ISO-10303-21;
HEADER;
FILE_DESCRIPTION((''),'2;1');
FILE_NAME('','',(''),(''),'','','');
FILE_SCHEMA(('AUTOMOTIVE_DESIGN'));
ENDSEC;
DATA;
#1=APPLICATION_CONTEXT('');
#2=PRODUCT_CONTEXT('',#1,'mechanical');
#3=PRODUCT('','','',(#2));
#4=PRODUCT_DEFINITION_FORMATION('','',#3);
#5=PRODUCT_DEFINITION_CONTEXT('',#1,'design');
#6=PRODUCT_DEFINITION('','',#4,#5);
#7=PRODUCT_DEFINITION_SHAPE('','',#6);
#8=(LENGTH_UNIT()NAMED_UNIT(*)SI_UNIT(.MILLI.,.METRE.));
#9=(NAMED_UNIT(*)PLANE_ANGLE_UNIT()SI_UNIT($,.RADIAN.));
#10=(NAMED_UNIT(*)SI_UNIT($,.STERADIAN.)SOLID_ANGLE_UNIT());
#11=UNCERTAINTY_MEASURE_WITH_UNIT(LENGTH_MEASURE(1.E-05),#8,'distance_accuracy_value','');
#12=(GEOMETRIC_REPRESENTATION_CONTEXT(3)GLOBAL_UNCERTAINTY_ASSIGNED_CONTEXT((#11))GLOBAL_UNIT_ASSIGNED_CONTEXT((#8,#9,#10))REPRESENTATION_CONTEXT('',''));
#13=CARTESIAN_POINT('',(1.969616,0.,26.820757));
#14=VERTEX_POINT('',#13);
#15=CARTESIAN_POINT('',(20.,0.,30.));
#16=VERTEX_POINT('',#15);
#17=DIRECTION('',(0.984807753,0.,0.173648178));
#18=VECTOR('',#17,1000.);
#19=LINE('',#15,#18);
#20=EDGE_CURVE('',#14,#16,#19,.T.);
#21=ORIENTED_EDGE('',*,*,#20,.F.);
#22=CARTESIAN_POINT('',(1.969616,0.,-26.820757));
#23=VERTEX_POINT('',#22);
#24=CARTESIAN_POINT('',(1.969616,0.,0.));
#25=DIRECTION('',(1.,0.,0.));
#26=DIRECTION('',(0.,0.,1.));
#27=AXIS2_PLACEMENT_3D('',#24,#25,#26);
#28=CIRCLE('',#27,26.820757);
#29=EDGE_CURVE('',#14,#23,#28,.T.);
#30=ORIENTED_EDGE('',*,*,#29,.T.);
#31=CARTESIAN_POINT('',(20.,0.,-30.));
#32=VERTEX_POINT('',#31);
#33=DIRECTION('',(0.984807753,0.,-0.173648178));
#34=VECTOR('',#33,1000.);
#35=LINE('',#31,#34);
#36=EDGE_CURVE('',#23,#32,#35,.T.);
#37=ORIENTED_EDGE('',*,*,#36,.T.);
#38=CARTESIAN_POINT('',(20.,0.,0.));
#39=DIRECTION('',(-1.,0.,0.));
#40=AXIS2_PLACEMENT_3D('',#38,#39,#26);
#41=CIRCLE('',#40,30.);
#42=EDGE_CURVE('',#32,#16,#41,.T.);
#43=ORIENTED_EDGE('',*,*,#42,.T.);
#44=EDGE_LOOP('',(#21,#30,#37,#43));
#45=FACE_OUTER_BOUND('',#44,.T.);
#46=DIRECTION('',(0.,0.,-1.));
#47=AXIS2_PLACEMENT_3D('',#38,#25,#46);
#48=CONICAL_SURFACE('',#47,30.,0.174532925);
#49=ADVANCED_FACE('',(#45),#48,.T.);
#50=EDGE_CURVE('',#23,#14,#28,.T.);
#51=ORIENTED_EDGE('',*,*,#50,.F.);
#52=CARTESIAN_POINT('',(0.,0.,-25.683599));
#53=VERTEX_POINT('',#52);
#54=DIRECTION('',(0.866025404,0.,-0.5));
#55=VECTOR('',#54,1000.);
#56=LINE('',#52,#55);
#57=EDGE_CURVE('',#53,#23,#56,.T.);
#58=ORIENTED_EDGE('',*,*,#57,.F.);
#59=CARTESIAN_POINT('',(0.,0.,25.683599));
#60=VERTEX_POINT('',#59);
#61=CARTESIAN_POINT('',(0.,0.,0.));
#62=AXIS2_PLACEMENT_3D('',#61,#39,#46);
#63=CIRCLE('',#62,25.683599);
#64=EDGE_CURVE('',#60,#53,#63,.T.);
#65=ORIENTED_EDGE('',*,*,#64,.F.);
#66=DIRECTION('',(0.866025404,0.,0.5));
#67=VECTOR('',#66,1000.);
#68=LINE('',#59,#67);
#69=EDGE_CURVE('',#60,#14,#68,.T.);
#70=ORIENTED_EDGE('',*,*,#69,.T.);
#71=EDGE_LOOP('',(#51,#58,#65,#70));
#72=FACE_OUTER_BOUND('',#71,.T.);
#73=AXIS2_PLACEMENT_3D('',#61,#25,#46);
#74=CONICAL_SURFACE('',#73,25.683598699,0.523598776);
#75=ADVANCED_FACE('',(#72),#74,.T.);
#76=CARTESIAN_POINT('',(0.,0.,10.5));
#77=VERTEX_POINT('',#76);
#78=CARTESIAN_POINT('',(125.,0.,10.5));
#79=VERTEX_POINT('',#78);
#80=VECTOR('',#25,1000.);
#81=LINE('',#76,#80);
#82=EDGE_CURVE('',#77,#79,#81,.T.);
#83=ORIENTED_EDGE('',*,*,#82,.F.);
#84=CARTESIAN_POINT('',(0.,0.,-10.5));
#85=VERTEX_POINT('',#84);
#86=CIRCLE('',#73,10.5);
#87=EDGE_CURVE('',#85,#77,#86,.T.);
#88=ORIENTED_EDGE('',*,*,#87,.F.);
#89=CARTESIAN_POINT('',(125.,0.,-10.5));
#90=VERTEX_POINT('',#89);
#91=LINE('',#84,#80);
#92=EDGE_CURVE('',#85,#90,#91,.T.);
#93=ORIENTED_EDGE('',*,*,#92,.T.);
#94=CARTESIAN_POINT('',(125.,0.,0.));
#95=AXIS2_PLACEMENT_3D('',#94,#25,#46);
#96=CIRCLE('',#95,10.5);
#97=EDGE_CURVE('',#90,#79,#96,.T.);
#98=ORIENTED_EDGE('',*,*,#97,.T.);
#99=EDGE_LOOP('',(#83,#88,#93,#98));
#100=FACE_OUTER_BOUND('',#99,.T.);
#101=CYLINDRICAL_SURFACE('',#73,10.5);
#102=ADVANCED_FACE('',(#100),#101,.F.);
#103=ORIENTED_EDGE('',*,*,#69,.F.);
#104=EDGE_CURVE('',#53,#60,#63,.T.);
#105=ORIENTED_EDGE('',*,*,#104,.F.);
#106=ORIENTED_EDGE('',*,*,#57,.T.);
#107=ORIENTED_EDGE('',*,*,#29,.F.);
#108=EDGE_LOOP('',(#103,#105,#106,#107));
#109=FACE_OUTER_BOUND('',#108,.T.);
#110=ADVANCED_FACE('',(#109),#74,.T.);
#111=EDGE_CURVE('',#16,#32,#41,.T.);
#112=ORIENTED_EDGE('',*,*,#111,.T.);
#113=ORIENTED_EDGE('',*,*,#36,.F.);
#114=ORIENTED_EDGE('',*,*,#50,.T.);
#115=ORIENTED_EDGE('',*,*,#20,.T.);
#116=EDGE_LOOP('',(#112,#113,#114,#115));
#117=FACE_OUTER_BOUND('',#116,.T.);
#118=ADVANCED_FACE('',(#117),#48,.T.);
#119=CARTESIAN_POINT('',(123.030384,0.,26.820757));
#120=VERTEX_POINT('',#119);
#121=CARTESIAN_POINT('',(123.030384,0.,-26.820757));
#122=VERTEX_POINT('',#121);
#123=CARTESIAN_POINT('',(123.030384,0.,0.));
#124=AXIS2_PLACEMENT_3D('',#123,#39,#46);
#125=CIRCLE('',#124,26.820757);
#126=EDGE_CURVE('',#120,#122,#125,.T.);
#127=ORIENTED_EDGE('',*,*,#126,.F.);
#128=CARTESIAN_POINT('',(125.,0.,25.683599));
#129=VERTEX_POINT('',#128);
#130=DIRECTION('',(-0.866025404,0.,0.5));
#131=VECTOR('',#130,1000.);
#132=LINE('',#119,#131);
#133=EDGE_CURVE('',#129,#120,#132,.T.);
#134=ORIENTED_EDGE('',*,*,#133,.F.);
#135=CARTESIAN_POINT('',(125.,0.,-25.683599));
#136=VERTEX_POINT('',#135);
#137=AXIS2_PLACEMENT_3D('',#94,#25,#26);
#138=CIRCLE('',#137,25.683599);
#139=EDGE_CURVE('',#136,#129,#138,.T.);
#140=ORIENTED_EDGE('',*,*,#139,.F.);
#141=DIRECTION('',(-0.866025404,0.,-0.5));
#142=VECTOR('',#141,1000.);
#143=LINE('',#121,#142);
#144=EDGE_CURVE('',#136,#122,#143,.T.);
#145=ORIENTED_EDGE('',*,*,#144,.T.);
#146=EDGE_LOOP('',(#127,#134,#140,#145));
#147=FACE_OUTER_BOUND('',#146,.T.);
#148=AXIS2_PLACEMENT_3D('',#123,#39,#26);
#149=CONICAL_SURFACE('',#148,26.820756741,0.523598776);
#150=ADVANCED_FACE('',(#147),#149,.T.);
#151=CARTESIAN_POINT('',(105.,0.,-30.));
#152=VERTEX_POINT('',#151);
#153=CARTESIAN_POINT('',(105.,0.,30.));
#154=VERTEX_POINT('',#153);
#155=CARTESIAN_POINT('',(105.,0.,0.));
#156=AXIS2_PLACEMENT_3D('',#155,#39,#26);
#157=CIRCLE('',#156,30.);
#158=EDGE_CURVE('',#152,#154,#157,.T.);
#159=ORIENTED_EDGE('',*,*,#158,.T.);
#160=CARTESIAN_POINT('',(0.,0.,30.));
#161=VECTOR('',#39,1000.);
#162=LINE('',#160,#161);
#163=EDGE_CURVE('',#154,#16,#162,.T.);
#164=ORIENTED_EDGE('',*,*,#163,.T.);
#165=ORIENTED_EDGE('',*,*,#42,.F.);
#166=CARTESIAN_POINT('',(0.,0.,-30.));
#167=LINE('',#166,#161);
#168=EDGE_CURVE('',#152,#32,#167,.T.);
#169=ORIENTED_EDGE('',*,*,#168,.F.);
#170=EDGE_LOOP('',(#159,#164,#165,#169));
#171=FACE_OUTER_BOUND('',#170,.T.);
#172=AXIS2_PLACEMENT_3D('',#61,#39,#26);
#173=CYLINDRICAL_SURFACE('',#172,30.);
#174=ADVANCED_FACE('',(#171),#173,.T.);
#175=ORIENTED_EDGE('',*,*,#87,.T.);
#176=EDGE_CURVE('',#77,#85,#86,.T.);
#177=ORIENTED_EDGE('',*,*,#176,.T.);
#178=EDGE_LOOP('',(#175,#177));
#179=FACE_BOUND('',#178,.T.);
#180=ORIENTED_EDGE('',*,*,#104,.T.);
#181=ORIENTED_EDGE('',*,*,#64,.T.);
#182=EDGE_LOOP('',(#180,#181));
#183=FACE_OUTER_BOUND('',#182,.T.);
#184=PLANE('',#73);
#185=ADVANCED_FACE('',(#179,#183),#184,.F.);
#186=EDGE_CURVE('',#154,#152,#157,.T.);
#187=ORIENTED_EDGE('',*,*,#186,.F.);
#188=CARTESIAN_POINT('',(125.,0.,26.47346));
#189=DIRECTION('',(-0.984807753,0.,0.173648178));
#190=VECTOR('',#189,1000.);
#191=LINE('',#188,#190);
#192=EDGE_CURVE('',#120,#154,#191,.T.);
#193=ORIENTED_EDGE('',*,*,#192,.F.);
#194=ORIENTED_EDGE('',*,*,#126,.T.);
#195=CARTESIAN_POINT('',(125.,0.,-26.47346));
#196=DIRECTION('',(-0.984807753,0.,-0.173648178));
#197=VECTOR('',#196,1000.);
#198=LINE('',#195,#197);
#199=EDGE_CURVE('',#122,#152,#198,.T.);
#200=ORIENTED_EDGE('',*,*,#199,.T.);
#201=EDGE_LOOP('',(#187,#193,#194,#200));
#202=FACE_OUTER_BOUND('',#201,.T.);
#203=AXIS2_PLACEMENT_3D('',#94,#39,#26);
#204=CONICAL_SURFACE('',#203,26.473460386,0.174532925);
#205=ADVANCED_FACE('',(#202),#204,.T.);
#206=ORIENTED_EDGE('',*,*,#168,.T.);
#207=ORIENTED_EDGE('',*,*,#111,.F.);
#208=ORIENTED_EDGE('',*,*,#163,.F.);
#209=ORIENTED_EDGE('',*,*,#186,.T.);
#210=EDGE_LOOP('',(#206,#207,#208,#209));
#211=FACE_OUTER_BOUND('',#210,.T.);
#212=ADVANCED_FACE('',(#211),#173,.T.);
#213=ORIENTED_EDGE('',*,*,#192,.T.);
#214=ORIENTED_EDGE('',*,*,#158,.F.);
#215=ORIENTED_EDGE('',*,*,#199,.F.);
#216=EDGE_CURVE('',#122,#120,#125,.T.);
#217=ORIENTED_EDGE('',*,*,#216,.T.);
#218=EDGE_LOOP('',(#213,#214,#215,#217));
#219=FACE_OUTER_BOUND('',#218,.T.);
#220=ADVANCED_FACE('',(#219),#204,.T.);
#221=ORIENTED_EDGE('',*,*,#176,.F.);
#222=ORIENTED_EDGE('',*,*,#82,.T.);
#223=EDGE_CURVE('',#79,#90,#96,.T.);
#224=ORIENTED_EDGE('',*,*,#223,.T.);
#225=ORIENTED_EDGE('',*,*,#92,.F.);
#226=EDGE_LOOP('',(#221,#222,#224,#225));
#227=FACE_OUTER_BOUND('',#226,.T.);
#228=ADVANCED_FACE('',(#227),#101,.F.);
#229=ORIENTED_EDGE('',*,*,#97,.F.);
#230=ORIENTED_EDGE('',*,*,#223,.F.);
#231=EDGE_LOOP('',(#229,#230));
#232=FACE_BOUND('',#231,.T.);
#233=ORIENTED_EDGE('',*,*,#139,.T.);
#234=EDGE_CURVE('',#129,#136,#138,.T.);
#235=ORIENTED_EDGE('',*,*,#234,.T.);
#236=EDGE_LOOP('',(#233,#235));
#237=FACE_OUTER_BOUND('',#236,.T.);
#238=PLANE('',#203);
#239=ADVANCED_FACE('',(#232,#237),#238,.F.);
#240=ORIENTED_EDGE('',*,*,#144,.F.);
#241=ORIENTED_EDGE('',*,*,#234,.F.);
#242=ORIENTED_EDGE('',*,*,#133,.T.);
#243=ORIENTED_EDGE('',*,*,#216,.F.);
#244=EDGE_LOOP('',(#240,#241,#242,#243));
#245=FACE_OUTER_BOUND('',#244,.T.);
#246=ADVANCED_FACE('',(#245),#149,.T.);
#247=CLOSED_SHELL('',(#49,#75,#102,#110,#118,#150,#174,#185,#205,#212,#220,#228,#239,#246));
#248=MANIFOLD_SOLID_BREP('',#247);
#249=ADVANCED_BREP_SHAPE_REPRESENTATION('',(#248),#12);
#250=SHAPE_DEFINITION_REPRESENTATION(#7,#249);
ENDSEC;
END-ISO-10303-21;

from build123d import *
from OCP.BRepFilletAPI import BRepFilletAPI_MakeChamfer

# Parameters (mm, degrees)
SKETCH_2_R              = 10.5
CUT_EXTRUDE_1_DEPTH     = 133.003787824
HOLE_WIZARD_M24_2_D     = 21
HOLE_WIZARD_M24_2_DEPTH = 63
HOLE_WIZARD_M24_2_TIP   = 6.3090365
CHAMFER_1_SIZE          = 2
CHAMFER_1_SIZE2         = 0.789861687


with BuildPart() as part:
    # 草图1 → 旋转1 (revolve)
    with BuildSketch(Plane.XY, mode=Mode.PRIVATE) as revolve_1_sk:
        Polygon((0, 0), (0, 26.473460386), (20, 30), (105, 30), (125, 26.473460386), (125, 0), align=None)
    revolve(revolve_1_sk.sketch.rotate(Axis((0, 0, 0), (1, 0, 0)), 90), axis=Axis((0, 0, 0), (1, 0, 0)))

    # 草图2 → 切除-拉伸1 (cut, through all)
    with BuildSketch(Plane(origin=(125, 0, 0), x_dir=(0, 0, -1), z_dir=(1, 0, 0))):
        Circle(SKETCH_2_R)
    extrude(amount=-CUT_EXTRUDE_1_DEPTH, mode=Mode.SUBTRACT)

    # M24 螺纹孔2
    with Locations(Plane(origin=(0, 0, 0), x_dir=(0, 0, -1), z_dir=(-1, 0, 0))):
        with Locations((0, 0)):
            Hole(HOLE_WIZARD_M24_2_D / 2, depth=HOLE_WIZARD_M24_2_DEPTH)
            with Locations((0, 0, -(HOLE_WIZARD_M24_2_DEPTH + HOLE_WIZARD_M24_2_TIP / 2))):  # 118° drill point
                Cone(0, HOLE_WIZARD_M24_2_D / 2, HOLE_WIZARD_M24_2_TIP, mode=Mode.SUBTRACT)

    # 倒角1: one chamfer whose edges measure the first distance from different faces: ONE call of the kernel's chamfer builder (chamfer() names one face for all edges)
    chamfer_1_edges_1 = [part.edges().sort_by_distance(p)[0] for p in [
        (0, 0, -26.473460386),
    ]]
    chamfer_1_side_1 = [part.faces().sort_by_distance(p)[0] for p in [
        (10, 0, -28.236730193),
    ]]
    chamfer_1_edges_2 = [part.edges().sort_by_distance(p)[0] for p in [
        (125, 0, -26.473460386),
    ]]
    chamfer_1_side_2 = [part.faces().sort_by_distance(p)[0] for p in [
        (115, 0, -28.236730193),
    ]]
    chamfer_1 = BRepFilletAPI_MakeChamfer(part.part.solid().wrapped)
    for e in chamfer_1_edges_1:
        chamfer_1.Add(CHAMFER_1_SIZE, CHAMFER_1_SIZE2, e.wrapped, chamfer_1_side_1[0].wrapped)  # the first distance lies on this face
    for e in chamfer_1_edges_2:
        chamfer_1.Add(CHAMFER_1_SIZE, CHAMFER_1_SIZE2, e.wrapped, chamfer_1_side_2[0].wrapped)  # the first distance lies on this face
    add(Compound.cast(chamfer_1.Shape()), mode=Mode.REPLACE)


solid = part.part
